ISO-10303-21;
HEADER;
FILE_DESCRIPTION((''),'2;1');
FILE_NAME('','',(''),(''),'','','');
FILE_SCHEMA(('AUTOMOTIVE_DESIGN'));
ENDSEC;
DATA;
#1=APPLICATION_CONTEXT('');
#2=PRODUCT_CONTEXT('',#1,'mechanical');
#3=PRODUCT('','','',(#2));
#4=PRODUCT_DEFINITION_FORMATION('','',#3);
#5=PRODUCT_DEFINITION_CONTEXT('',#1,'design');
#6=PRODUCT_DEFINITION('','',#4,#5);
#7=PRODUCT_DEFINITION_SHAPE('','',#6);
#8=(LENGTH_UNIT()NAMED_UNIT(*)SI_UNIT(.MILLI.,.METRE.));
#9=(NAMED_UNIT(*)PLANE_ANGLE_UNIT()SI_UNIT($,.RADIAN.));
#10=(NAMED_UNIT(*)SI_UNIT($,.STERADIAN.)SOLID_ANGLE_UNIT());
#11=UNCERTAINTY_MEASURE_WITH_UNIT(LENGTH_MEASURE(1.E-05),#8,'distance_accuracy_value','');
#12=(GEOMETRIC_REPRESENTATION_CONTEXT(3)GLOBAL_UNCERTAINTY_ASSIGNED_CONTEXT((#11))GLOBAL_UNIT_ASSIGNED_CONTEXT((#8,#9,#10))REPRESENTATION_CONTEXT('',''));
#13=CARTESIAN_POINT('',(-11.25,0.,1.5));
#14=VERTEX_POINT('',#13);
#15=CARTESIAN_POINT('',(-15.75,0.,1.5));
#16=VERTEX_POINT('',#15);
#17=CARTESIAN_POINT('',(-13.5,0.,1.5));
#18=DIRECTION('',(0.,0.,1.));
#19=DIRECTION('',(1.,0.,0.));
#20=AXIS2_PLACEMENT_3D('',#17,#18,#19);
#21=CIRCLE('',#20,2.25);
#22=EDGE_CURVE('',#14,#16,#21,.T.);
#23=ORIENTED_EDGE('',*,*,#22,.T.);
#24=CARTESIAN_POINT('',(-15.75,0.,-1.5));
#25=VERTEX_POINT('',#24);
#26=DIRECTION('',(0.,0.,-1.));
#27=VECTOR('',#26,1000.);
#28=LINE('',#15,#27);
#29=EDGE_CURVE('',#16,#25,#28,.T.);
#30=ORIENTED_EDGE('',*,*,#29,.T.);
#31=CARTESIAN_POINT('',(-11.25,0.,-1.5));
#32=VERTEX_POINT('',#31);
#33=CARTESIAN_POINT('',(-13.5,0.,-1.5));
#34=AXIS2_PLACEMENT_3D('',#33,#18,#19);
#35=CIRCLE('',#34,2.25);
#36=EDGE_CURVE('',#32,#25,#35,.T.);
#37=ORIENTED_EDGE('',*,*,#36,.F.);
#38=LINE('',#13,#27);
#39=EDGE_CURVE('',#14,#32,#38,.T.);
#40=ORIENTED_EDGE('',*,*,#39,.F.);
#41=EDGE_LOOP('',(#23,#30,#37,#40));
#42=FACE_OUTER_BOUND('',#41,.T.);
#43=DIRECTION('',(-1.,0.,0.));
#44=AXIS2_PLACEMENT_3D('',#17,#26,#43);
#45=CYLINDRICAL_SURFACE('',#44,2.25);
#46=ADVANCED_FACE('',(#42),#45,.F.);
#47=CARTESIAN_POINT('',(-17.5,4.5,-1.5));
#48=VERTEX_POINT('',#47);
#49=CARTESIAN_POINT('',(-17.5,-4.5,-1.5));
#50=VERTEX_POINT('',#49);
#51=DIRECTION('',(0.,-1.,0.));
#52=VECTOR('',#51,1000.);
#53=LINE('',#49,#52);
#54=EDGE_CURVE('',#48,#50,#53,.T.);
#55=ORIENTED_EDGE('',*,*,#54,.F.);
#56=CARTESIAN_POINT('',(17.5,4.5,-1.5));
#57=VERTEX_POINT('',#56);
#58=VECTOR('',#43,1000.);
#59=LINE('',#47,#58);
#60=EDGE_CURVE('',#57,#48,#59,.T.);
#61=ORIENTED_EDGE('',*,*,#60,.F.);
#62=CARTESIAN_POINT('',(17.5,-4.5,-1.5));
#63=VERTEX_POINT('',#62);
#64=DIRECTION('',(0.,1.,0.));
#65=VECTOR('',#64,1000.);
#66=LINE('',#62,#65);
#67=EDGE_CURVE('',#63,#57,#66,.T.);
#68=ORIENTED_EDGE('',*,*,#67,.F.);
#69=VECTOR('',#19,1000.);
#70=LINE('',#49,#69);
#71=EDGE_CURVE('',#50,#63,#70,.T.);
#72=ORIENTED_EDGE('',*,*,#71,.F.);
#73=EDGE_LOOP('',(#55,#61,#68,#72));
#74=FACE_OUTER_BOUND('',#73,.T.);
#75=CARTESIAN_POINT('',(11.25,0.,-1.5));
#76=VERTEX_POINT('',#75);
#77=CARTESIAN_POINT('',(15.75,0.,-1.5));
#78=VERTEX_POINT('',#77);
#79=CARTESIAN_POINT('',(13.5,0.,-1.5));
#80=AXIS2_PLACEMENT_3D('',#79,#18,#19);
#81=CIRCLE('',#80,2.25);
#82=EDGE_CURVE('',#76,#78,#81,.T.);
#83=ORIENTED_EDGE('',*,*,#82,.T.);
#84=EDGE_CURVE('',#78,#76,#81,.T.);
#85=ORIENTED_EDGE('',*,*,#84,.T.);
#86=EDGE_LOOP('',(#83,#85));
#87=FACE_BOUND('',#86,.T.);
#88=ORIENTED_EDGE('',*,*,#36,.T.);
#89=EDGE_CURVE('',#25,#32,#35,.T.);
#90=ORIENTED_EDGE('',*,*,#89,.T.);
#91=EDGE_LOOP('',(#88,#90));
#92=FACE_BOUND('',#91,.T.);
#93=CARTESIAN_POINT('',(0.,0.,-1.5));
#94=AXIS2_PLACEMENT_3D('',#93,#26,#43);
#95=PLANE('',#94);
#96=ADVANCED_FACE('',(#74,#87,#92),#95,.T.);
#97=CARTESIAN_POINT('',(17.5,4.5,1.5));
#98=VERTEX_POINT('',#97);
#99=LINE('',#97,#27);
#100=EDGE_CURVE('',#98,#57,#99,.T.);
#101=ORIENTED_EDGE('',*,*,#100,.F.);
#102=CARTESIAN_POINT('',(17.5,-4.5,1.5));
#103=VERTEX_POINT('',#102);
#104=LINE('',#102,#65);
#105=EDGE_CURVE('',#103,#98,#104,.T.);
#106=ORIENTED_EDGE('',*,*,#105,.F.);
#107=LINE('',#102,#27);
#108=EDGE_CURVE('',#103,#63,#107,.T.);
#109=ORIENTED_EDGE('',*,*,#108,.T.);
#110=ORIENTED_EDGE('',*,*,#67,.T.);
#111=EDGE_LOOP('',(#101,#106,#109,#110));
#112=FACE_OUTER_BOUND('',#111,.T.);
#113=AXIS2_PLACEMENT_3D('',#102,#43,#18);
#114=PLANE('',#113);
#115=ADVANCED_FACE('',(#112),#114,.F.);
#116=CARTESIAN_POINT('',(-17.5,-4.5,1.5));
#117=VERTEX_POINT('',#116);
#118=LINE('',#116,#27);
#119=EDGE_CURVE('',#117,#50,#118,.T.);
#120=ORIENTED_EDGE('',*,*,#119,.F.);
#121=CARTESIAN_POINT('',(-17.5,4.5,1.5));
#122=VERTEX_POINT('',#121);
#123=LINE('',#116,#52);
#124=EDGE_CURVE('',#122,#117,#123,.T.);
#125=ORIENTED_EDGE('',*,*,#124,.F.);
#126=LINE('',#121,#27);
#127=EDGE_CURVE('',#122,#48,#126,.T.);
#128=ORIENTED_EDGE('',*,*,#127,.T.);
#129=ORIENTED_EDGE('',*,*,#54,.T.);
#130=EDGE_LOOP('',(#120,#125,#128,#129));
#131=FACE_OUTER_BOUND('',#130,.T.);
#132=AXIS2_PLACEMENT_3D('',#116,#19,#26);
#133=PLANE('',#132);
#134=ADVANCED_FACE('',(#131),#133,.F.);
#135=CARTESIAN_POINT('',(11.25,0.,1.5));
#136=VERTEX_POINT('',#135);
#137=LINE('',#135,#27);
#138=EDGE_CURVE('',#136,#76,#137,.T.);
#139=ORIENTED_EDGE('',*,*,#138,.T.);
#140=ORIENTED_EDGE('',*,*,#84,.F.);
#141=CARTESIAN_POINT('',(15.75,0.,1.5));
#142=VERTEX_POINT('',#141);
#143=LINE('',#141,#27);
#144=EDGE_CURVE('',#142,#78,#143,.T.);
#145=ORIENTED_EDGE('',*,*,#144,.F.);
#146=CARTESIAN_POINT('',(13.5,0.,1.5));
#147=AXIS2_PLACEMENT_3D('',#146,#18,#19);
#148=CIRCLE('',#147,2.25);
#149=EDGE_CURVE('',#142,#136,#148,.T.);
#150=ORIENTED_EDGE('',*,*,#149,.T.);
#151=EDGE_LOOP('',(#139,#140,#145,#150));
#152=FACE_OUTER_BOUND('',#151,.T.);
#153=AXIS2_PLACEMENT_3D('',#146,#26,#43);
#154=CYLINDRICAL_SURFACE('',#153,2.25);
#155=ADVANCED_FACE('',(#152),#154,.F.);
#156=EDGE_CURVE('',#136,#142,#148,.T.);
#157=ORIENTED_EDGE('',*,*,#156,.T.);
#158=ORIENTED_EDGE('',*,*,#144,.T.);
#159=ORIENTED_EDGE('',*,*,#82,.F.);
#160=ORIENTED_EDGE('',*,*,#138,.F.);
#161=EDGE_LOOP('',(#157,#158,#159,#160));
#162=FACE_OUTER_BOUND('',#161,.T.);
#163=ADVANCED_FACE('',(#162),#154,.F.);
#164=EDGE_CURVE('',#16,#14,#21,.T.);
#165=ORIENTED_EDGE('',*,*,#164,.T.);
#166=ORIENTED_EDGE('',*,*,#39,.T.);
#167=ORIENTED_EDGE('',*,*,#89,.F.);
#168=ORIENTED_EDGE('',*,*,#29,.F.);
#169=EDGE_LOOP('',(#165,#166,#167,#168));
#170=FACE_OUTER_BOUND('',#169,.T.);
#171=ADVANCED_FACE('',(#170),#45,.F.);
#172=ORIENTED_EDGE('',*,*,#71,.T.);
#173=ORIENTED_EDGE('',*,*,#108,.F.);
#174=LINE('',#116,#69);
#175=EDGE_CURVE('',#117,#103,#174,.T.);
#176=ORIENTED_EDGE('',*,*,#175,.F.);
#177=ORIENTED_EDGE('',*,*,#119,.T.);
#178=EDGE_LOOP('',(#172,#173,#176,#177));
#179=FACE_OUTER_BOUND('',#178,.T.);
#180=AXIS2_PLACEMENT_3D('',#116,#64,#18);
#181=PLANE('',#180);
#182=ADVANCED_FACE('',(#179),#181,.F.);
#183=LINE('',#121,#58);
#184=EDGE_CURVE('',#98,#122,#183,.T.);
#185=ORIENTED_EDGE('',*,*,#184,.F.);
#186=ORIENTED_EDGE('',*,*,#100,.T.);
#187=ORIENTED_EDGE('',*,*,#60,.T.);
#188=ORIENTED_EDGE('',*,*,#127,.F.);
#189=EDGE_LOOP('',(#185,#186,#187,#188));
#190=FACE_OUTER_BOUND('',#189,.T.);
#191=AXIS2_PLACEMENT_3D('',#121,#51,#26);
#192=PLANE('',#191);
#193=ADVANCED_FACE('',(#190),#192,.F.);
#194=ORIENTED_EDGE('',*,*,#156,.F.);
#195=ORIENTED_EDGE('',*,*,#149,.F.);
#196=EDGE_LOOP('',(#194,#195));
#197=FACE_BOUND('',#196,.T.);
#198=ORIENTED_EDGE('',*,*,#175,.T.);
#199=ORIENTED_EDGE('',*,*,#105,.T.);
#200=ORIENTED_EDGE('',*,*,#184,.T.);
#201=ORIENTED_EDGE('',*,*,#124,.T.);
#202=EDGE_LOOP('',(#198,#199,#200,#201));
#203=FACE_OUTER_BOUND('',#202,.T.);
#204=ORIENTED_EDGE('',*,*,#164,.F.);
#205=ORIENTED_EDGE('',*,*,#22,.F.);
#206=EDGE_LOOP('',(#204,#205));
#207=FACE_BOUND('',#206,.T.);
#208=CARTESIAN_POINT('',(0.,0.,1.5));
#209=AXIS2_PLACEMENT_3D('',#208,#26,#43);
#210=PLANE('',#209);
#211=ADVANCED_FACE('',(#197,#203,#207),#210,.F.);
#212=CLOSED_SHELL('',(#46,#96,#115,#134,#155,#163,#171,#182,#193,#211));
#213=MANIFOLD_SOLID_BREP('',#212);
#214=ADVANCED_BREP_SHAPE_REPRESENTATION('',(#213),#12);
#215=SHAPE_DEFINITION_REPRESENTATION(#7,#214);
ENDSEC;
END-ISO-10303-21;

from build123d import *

# Parameters (mm, degrees)
SKETCH_1_W      = 35
SKETCH_1_H      = 9
SKETCH_1_R      = 2.25
EXTRUDE_1_DEPTH = 1.5


with BuildPart() as part:
    # 草图1 → 凸台-拉伸1 (new, symmetric)
    with BuildSketch(Plane.XY):
        Rectangle(SKETCH_1_W, SKETCH_1_H)
        with Locations((-13.5, 0)):
            Circle(SKETCH_1_R, mode=Mode.SUBTRACT)
        with Locations((13.5, 0)):
            Circle(SKETCH_1_R, mode=Mode.SUBTRACT)
    extrude(amount=EXTRUDE_1_DEPTH, both=True)


solid = part.part
